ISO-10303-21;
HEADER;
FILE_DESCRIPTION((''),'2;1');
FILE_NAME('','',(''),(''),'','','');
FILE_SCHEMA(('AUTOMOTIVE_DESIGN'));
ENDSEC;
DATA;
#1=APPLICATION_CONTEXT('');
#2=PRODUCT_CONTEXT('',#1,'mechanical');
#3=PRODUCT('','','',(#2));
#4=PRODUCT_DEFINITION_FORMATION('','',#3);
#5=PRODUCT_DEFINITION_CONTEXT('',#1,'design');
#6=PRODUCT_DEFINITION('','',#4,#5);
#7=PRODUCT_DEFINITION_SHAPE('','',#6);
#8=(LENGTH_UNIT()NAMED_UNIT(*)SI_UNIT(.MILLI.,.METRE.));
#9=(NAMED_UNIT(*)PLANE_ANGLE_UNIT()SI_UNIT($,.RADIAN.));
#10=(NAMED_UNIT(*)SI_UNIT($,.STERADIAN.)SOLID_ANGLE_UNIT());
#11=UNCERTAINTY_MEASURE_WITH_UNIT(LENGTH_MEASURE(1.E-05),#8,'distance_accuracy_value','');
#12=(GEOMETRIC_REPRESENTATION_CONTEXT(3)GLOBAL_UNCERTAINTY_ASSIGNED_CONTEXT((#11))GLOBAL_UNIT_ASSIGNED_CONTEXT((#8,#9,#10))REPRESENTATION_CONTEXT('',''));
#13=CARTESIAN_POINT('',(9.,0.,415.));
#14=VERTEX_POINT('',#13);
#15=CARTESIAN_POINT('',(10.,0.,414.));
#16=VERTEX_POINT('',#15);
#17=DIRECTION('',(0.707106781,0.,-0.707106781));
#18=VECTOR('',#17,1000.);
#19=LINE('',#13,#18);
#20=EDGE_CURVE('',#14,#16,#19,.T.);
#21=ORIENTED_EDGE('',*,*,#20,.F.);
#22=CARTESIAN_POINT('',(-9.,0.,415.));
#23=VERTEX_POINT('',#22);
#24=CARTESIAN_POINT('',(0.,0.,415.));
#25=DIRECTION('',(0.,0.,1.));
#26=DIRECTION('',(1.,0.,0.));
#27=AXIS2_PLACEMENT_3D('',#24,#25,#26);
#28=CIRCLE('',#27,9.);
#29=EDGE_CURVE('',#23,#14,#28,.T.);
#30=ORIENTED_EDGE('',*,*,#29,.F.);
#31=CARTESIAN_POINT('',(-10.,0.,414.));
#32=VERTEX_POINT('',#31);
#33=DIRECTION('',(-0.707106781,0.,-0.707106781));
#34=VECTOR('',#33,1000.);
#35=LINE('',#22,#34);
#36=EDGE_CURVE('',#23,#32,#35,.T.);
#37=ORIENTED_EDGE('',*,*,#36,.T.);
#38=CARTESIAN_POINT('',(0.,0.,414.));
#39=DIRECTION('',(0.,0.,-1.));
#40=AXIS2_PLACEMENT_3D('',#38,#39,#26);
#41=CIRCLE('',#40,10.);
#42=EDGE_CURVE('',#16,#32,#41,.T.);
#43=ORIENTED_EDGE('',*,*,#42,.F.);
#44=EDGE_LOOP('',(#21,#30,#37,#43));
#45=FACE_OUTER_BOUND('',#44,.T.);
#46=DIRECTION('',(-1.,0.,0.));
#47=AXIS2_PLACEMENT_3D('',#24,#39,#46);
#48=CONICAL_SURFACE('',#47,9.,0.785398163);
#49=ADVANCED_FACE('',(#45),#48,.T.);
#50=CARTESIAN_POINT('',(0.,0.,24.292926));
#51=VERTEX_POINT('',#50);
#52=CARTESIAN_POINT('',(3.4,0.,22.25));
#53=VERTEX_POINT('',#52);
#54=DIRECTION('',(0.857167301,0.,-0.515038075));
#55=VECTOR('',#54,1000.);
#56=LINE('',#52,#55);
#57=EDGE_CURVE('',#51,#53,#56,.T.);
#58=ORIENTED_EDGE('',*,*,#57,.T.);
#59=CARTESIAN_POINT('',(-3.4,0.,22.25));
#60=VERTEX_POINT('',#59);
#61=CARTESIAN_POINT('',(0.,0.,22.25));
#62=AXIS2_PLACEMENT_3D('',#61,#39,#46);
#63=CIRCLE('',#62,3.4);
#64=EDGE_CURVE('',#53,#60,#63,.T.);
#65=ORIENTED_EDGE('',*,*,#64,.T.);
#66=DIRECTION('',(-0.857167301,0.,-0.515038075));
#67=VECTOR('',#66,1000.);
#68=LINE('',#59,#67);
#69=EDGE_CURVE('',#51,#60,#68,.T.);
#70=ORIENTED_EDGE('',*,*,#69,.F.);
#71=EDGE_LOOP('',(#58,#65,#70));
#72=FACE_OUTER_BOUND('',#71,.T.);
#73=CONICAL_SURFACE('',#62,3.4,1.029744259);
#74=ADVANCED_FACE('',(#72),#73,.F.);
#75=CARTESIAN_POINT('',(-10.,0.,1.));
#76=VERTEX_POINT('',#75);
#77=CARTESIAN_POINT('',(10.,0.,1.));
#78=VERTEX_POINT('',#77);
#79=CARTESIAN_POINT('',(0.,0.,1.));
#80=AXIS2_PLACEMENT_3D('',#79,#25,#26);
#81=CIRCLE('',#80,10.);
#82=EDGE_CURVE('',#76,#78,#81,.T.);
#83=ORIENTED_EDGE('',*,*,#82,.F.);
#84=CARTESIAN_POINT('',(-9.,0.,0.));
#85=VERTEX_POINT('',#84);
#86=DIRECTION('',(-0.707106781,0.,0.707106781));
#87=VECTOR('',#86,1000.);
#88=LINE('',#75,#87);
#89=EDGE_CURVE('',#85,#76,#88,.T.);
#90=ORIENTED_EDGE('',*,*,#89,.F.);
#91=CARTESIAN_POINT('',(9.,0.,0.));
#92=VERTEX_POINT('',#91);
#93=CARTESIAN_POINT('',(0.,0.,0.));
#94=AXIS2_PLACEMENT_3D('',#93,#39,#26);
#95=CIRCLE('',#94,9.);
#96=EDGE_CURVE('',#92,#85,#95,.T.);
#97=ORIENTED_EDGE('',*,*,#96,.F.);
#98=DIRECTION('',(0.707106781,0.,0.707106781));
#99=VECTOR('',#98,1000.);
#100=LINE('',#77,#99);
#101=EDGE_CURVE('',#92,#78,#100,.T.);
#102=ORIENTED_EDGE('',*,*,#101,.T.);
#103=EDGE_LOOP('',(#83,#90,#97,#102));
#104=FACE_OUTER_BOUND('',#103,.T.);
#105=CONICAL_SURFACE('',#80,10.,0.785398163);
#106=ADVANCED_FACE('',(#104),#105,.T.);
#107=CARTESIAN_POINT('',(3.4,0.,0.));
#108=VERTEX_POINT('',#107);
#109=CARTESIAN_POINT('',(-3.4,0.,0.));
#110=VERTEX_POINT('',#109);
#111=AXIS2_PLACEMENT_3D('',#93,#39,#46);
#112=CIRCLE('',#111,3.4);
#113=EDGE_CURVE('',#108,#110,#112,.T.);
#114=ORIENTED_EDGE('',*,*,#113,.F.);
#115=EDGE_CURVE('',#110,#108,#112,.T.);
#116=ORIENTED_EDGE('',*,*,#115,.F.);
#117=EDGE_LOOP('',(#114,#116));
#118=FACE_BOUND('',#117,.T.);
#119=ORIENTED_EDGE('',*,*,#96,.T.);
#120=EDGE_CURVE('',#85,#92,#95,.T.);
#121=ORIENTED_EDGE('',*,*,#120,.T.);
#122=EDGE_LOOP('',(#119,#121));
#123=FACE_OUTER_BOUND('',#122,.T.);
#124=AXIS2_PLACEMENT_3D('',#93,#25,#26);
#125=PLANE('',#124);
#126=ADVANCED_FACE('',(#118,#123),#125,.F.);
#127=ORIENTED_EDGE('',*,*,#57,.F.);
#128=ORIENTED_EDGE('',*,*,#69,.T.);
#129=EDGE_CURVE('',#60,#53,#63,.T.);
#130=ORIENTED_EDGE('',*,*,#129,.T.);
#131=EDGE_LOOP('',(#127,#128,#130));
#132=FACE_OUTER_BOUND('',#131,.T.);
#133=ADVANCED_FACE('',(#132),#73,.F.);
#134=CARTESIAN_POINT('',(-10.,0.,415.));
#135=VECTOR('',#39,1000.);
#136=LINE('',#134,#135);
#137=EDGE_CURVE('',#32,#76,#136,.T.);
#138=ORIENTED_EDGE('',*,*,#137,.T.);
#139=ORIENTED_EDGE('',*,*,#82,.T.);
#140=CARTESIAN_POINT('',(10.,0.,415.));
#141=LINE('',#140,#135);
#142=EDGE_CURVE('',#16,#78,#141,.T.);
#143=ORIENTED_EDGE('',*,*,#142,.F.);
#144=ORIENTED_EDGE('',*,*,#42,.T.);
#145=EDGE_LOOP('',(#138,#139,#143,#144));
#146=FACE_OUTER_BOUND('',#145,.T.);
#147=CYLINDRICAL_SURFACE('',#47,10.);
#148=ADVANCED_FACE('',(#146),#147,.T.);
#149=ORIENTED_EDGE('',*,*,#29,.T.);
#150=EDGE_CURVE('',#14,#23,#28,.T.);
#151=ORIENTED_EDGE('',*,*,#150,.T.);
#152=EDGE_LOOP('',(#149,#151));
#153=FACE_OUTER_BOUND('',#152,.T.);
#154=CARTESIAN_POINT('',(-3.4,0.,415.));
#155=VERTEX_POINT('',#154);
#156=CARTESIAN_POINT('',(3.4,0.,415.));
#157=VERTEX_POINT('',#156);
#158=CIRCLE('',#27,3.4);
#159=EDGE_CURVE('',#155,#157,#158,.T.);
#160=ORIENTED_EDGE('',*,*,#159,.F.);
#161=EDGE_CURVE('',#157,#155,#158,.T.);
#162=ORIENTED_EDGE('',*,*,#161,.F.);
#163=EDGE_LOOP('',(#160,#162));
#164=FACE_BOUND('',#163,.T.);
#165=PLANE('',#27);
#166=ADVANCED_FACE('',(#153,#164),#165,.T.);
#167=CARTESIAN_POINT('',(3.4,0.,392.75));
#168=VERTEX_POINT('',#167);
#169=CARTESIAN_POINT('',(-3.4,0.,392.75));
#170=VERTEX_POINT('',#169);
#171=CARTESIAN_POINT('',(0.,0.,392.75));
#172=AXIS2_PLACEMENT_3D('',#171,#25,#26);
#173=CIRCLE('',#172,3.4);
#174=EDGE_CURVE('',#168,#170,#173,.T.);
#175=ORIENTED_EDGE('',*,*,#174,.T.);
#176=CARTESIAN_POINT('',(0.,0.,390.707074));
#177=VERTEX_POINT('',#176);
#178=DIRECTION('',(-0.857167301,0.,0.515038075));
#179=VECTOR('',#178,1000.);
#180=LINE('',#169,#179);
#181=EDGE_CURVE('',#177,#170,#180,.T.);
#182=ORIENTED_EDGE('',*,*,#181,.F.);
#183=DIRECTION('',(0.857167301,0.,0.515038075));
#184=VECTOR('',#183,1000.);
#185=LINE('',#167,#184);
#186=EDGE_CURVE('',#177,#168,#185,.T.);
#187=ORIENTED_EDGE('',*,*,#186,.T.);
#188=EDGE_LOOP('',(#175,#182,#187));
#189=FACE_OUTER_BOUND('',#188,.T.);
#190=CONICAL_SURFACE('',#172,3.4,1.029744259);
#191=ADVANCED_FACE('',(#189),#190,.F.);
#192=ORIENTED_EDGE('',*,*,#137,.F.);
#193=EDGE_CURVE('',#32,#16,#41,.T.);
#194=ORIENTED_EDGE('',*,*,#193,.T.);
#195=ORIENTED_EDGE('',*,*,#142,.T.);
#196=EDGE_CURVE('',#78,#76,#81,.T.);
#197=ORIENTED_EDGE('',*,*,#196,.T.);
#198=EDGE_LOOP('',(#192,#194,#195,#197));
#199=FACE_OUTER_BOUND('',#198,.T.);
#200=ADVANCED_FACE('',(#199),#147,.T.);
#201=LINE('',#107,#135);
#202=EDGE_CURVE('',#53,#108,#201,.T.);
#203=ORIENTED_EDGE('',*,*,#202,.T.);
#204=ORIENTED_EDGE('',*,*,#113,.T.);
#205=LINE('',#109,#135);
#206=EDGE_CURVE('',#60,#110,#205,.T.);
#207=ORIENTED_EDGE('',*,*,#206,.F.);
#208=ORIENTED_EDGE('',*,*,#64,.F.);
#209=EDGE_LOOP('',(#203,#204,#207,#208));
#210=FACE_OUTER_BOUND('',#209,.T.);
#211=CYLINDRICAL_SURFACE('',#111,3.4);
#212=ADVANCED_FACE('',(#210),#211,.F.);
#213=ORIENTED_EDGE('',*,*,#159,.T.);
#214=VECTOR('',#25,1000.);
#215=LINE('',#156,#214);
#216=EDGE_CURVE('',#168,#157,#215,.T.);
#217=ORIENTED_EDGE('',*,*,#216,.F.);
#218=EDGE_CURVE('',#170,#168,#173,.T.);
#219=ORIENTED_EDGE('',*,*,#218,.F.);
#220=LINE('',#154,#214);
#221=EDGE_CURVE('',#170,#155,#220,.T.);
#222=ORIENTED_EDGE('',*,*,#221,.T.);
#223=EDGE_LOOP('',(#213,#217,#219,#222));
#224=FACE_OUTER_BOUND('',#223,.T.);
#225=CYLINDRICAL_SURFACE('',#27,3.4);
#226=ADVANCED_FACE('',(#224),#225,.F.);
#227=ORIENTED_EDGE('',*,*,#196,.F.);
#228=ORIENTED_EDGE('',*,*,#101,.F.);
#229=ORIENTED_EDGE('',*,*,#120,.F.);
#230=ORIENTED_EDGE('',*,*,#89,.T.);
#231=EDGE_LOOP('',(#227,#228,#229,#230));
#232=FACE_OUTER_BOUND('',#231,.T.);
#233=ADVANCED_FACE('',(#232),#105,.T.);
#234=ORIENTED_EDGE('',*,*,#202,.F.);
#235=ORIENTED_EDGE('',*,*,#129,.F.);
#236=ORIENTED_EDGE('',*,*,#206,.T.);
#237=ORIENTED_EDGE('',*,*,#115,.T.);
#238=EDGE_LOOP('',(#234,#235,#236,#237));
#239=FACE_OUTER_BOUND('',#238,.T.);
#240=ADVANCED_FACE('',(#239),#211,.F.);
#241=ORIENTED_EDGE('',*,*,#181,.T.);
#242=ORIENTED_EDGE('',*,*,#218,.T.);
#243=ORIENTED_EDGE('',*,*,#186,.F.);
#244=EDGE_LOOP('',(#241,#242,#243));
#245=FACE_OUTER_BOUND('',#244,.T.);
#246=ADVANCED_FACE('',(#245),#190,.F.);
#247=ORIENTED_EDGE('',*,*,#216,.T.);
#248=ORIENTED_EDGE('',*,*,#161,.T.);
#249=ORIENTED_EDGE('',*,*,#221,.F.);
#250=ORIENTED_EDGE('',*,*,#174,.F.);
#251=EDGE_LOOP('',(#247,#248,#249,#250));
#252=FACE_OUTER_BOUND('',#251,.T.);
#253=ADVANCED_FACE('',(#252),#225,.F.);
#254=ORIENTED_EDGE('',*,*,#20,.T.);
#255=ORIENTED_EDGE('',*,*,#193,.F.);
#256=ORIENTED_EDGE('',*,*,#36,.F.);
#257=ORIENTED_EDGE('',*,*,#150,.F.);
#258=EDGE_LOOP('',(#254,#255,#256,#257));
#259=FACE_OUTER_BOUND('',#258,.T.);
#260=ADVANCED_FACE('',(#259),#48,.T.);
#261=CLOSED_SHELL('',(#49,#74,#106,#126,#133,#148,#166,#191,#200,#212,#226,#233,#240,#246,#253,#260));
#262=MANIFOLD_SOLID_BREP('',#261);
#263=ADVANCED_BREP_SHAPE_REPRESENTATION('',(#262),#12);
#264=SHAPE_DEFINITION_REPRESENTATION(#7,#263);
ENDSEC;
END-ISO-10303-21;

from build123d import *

# Parameters (mm, degrees)
SKETCH_1_R             = 10
EXTRUDE_1_DEPTH        = 415
HOLE_WIZARD_M8_1_D     = 6.8
HOLE_WIZARD_M8_1_DEPTH = 22.25
HOLE_WIZARD_M8_1_TIP   = 2.042926105
CHAMFER_1_SIZE         = 1
HOLE_WIZARD_M8_2_D     = 6.8
HOLE_WIZARD_M8_2_DEPTH = 22.25
HOLE_WIZARD_M8_2_TIP   = 2.042926105


with BuildPart() as part:
    # 草图1 → 凸台-拉伸1 (new body)
    with BuildSketch(Plane.XY):
        Circle(SKETCH_1_R)
    extrude(amount=EXTRUDE_1_DEPTH)

    # M8 螺纹孔1
    with Locations(Plane.XY.offset(415)):
        with Locations((0, 0)):
            Hole(HOLE_WIZARD_M8_1_D / 2, depth=HOLE_WIZARD_M8_1_DEPTH)
            with Locations((0, 0, -(HOLE_WIZARD_M8_1_DEPTH + HOLE_WIZARD_M8_1_TIP / 2))):  # 118° drill point
                Cone(0, HOLE_WIZARD_M8_1_D / 2, HOLE_WIZARD_M8_1_TIP, mode=Mode.SUBTRACT)

    # 倒角1
    chamfer_1_edges = [part.edges().sort_by_distance(p)[0] for p in [
        (-10, 0, 0),
        (-10, 0, 415),
    ]]
    chamfer(chamfer_1_edges, length=CHAMFER_1_SIZE)

    # M8 螺纹孔2
    with Locations(Plane(origin=(0, 0, 0), x_dir=(-1, 0, 0), z_dir=(0, 0, -1))):
        with Locations((0, 0)):
            Hole(HOLE_WIZARD_M8_2_D / 2, depth=HOLE_WIZARD_M8_2_DEPTH)
            with Locations((0, 0, -(HOLE_WIZARD_M8_2_DEPTH + HOLE_WIZARD_M8_2_TIP / 2))):  # 118° drill point
                Cone(0, HOLE_WIZARD_M8_2_D / 2, HOLE_WIZARD_M8_2_TIP, mode=Mode.SUBTRACT)


solid = part.part
